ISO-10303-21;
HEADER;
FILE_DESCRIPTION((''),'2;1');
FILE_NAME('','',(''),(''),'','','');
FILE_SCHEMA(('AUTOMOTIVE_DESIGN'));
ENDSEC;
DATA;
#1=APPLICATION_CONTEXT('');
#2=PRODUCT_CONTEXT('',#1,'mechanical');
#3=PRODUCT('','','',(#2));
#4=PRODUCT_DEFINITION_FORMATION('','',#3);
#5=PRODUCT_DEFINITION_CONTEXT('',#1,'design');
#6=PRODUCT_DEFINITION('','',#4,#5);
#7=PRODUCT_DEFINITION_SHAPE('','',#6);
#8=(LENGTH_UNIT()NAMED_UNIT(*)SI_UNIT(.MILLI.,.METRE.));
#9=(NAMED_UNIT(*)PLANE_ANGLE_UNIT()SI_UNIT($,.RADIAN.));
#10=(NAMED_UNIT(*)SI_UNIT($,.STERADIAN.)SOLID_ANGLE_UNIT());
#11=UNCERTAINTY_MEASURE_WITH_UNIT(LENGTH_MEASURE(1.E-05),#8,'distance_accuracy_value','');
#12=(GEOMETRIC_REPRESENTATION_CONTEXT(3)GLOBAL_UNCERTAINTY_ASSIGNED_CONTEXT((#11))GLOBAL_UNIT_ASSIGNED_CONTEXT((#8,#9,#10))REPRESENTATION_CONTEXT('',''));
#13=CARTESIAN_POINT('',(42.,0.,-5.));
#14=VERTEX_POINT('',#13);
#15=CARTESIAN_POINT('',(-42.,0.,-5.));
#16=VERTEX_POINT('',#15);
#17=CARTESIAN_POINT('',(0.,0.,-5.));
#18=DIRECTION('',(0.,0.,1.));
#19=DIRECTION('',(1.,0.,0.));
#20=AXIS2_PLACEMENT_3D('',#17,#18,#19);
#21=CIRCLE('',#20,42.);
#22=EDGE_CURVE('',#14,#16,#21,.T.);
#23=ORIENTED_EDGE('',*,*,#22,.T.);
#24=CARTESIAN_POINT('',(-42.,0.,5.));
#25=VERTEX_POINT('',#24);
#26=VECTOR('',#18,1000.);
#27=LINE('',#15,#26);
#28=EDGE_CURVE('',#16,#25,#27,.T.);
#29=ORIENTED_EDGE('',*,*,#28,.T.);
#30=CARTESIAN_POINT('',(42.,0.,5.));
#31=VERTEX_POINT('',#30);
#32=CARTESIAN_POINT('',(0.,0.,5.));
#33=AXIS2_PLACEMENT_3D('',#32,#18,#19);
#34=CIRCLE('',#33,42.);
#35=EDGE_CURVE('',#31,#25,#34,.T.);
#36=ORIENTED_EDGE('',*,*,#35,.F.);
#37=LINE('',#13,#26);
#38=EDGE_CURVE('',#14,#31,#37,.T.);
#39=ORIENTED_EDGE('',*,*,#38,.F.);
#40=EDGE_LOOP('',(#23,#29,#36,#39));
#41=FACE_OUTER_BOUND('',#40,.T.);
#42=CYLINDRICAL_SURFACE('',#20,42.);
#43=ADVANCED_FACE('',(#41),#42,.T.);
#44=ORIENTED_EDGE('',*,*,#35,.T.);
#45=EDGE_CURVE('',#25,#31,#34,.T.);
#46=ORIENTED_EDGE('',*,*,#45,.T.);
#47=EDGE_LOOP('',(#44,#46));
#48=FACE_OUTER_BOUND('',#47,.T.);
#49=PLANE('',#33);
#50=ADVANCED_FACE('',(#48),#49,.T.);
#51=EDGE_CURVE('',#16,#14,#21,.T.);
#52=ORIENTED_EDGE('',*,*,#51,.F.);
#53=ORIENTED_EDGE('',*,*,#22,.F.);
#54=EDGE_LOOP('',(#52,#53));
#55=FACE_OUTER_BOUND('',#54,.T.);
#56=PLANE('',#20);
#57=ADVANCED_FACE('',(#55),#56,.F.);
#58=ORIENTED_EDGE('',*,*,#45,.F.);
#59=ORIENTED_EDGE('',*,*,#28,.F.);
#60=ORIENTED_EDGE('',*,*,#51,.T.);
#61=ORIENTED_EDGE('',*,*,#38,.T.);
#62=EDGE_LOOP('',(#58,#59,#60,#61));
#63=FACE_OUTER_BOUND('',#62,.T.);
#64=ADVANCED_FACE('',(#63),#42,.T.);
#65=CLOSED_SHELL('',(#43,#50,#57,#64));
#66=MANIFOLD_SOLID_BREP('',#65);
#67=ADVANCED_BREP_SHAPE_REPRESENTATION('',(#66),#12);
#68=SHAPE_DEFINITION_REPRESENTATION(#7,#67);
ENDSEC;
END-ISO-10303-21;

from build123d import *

# Parameters (mm, degrees)
SKETCH_1_R      = 42
EXTRUDE_1_DEPTH = 5


with BuildPart() as part:
    # 草图1 → 凸台-拉伸1 (new, symmetric)
    with BuildSketch(Plane.XY):
        Circle(SKETCH_1_R)
    extrude(amount=EXTRUDE_1_DEPTH, both=True)


solid = part.part
